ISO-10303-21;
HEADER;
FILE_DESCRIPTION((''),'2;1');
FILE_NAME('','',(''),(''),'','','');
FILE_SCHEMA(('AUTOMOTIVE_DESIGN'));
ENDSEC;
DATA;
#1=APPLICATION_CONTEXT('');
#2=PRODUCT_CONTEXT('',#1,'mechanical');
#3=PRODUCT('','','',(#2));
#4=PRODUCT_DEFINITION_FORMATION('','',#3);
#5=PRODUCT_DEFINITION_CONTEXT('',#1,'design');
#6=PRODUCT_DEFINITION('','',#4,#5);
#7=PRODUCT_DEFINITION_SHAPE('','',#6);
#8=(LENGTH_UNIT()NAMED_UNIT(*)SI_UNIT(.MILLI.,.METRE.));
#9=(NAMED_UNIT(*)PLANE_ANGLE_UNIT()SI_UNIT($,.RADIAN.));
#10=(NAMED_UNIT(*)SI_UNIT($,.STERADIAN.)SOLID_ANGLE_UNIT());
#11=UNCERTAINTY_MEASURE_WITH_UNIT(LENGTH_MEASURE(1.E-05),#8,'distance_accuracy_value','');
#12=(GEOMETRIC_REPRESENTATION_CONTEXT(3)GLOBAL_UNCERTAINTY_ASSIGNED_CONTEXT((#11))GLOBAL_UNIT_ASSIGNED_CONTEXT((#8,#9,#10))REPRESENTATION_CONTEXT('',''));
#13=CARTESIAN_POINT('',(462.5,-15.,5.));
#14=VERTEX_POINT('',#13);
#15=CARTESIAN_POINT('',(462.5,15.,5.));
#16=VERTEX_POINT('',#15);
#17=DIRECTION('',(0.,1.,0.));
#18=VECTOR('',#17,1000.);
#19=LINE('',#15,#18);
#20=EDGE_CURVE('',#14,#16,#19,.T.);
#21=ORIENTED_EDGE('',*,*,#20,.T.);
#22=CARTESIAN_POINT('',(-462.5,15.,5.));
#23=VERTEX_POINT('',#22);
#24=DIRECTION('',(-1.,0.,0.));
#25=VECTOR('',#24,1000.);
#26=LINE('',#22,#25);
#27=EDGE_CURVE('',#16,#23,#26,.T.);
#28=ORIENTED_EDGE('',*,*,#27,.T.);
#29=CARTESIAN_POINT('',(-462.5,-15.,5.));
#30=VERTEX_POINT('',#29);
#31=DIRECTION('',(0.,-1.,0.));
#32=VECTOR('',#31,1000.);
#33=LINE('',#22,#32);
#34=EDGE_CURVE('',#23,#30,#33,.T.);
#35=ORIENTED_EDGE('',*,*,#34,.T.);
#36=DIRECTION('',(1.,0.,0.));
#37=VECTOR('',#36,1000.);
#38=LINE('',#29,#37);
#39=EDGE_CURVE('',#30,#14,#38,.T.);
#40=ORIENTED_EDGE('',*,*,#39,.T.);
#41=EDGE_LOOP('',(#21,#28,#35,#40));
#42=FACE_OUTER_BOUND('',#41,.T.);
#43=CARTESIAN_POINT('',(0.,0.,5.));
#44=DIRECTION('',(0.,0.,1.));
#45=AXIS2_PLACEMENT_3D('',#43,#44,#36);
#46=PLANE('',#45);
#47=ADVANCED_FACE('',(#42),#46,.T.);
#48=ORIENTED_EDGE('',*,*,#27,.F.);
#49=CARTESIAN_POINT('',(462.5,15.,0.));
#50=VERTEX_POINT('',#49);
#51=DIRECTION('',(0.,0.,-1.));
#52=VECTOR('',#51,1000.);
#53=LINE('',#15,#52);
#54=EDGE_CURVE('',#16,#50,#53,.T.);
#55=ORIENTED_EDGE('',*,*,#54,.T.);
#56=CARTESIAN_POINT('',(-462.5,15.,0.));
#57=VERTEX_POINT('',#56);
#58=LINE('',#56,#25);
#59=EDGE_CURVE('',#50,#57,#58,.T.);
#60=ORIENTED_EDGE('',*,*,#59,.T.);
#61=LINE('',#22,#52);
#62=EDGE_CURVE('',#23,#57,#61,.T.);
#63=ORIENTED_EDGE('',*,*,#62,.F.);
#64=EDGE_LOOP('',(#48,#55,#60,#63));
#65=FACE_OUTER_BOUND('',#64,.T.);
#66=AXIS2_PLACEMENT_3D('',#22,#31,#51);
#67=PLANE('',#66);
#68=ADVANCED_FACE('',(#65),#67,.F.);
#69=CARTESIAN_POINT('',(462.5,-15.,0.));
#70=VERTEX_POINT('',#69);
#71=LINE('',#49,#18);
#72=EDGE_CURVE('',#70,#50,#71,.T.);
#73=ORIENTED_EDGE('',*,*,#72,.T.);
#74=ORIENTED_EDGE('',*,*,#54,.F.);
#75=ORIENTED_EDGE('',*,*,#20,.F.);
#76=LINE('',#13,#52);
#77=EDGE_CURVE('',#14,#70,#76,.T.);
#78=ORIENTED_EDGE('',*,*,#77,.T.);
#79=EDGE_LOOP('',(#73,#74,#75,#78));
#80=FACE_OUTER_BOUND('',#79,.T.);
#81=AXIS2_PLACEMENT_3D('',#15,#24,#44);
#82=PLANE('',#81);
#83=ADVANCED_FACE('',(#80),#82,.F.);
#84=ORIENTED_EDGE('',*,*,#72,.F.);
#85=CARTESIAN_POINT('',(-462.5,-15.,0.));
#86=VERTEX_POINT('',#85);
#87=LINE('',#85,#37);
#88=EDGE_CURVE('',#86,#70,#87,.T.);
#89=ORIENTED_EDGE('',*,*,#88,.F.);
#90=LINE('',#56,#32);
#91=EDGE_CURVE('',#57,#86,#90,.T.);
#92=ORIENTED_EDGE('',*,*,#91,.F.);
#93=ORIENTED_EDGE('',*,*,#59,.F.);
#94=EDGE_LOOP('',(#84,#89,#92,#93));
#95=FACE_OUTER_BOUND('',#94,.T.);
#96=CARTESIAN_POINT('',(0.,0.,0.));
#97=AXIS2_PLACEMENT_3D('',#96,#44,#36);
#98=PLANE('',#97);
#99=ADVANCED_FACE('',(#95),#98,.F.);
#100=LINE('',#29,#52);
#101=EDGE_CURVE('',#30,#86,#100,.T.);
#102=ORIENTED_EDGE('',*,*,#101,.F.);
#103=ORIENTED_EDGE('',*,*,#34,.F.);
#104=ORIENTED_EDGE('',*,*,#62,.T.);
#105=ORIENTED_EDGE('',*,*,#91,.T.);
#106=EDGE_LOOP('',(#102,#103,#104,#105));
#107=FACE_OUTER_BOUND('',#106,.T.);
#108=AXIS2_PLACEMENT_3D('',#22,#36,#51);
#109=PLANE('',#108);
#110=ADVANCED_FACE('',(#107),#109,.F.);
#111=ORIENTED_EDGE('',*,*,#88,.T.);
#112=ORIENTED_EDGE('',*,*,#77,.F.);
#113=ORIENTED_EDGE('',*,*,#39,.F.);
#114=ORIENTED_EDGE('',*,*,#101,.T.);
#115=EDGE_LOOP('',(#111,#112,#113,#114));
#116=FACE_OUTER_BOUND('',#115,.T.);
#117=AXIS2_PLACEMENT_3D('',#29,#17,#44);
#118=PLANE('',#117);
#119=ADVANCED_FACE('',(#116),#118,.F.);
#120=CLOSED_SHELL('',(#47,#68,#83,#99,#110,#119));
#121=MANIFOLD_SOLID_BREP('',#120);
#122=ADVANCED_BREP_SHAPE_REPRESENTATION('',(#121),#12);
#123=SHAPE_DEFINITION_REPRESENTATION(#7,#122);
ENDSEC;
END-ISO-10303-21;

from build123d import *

# Parameters (mm, degrees)
SKETCH1_W           = 925
SKETCH1_H           = 30
BOSS_EXTRUDE1_DEPTH = 5


with BuildPart() as part:
    # Sketch1 → Boss-Extrude1 (new body)
    with BuildSketch(Plane.XY):
        Rectangle(SKETCH1_W, SKETCH1_H)
    extrude(amount=BOSS_EXTRUDE1_DEPTH)


solid = part.part
